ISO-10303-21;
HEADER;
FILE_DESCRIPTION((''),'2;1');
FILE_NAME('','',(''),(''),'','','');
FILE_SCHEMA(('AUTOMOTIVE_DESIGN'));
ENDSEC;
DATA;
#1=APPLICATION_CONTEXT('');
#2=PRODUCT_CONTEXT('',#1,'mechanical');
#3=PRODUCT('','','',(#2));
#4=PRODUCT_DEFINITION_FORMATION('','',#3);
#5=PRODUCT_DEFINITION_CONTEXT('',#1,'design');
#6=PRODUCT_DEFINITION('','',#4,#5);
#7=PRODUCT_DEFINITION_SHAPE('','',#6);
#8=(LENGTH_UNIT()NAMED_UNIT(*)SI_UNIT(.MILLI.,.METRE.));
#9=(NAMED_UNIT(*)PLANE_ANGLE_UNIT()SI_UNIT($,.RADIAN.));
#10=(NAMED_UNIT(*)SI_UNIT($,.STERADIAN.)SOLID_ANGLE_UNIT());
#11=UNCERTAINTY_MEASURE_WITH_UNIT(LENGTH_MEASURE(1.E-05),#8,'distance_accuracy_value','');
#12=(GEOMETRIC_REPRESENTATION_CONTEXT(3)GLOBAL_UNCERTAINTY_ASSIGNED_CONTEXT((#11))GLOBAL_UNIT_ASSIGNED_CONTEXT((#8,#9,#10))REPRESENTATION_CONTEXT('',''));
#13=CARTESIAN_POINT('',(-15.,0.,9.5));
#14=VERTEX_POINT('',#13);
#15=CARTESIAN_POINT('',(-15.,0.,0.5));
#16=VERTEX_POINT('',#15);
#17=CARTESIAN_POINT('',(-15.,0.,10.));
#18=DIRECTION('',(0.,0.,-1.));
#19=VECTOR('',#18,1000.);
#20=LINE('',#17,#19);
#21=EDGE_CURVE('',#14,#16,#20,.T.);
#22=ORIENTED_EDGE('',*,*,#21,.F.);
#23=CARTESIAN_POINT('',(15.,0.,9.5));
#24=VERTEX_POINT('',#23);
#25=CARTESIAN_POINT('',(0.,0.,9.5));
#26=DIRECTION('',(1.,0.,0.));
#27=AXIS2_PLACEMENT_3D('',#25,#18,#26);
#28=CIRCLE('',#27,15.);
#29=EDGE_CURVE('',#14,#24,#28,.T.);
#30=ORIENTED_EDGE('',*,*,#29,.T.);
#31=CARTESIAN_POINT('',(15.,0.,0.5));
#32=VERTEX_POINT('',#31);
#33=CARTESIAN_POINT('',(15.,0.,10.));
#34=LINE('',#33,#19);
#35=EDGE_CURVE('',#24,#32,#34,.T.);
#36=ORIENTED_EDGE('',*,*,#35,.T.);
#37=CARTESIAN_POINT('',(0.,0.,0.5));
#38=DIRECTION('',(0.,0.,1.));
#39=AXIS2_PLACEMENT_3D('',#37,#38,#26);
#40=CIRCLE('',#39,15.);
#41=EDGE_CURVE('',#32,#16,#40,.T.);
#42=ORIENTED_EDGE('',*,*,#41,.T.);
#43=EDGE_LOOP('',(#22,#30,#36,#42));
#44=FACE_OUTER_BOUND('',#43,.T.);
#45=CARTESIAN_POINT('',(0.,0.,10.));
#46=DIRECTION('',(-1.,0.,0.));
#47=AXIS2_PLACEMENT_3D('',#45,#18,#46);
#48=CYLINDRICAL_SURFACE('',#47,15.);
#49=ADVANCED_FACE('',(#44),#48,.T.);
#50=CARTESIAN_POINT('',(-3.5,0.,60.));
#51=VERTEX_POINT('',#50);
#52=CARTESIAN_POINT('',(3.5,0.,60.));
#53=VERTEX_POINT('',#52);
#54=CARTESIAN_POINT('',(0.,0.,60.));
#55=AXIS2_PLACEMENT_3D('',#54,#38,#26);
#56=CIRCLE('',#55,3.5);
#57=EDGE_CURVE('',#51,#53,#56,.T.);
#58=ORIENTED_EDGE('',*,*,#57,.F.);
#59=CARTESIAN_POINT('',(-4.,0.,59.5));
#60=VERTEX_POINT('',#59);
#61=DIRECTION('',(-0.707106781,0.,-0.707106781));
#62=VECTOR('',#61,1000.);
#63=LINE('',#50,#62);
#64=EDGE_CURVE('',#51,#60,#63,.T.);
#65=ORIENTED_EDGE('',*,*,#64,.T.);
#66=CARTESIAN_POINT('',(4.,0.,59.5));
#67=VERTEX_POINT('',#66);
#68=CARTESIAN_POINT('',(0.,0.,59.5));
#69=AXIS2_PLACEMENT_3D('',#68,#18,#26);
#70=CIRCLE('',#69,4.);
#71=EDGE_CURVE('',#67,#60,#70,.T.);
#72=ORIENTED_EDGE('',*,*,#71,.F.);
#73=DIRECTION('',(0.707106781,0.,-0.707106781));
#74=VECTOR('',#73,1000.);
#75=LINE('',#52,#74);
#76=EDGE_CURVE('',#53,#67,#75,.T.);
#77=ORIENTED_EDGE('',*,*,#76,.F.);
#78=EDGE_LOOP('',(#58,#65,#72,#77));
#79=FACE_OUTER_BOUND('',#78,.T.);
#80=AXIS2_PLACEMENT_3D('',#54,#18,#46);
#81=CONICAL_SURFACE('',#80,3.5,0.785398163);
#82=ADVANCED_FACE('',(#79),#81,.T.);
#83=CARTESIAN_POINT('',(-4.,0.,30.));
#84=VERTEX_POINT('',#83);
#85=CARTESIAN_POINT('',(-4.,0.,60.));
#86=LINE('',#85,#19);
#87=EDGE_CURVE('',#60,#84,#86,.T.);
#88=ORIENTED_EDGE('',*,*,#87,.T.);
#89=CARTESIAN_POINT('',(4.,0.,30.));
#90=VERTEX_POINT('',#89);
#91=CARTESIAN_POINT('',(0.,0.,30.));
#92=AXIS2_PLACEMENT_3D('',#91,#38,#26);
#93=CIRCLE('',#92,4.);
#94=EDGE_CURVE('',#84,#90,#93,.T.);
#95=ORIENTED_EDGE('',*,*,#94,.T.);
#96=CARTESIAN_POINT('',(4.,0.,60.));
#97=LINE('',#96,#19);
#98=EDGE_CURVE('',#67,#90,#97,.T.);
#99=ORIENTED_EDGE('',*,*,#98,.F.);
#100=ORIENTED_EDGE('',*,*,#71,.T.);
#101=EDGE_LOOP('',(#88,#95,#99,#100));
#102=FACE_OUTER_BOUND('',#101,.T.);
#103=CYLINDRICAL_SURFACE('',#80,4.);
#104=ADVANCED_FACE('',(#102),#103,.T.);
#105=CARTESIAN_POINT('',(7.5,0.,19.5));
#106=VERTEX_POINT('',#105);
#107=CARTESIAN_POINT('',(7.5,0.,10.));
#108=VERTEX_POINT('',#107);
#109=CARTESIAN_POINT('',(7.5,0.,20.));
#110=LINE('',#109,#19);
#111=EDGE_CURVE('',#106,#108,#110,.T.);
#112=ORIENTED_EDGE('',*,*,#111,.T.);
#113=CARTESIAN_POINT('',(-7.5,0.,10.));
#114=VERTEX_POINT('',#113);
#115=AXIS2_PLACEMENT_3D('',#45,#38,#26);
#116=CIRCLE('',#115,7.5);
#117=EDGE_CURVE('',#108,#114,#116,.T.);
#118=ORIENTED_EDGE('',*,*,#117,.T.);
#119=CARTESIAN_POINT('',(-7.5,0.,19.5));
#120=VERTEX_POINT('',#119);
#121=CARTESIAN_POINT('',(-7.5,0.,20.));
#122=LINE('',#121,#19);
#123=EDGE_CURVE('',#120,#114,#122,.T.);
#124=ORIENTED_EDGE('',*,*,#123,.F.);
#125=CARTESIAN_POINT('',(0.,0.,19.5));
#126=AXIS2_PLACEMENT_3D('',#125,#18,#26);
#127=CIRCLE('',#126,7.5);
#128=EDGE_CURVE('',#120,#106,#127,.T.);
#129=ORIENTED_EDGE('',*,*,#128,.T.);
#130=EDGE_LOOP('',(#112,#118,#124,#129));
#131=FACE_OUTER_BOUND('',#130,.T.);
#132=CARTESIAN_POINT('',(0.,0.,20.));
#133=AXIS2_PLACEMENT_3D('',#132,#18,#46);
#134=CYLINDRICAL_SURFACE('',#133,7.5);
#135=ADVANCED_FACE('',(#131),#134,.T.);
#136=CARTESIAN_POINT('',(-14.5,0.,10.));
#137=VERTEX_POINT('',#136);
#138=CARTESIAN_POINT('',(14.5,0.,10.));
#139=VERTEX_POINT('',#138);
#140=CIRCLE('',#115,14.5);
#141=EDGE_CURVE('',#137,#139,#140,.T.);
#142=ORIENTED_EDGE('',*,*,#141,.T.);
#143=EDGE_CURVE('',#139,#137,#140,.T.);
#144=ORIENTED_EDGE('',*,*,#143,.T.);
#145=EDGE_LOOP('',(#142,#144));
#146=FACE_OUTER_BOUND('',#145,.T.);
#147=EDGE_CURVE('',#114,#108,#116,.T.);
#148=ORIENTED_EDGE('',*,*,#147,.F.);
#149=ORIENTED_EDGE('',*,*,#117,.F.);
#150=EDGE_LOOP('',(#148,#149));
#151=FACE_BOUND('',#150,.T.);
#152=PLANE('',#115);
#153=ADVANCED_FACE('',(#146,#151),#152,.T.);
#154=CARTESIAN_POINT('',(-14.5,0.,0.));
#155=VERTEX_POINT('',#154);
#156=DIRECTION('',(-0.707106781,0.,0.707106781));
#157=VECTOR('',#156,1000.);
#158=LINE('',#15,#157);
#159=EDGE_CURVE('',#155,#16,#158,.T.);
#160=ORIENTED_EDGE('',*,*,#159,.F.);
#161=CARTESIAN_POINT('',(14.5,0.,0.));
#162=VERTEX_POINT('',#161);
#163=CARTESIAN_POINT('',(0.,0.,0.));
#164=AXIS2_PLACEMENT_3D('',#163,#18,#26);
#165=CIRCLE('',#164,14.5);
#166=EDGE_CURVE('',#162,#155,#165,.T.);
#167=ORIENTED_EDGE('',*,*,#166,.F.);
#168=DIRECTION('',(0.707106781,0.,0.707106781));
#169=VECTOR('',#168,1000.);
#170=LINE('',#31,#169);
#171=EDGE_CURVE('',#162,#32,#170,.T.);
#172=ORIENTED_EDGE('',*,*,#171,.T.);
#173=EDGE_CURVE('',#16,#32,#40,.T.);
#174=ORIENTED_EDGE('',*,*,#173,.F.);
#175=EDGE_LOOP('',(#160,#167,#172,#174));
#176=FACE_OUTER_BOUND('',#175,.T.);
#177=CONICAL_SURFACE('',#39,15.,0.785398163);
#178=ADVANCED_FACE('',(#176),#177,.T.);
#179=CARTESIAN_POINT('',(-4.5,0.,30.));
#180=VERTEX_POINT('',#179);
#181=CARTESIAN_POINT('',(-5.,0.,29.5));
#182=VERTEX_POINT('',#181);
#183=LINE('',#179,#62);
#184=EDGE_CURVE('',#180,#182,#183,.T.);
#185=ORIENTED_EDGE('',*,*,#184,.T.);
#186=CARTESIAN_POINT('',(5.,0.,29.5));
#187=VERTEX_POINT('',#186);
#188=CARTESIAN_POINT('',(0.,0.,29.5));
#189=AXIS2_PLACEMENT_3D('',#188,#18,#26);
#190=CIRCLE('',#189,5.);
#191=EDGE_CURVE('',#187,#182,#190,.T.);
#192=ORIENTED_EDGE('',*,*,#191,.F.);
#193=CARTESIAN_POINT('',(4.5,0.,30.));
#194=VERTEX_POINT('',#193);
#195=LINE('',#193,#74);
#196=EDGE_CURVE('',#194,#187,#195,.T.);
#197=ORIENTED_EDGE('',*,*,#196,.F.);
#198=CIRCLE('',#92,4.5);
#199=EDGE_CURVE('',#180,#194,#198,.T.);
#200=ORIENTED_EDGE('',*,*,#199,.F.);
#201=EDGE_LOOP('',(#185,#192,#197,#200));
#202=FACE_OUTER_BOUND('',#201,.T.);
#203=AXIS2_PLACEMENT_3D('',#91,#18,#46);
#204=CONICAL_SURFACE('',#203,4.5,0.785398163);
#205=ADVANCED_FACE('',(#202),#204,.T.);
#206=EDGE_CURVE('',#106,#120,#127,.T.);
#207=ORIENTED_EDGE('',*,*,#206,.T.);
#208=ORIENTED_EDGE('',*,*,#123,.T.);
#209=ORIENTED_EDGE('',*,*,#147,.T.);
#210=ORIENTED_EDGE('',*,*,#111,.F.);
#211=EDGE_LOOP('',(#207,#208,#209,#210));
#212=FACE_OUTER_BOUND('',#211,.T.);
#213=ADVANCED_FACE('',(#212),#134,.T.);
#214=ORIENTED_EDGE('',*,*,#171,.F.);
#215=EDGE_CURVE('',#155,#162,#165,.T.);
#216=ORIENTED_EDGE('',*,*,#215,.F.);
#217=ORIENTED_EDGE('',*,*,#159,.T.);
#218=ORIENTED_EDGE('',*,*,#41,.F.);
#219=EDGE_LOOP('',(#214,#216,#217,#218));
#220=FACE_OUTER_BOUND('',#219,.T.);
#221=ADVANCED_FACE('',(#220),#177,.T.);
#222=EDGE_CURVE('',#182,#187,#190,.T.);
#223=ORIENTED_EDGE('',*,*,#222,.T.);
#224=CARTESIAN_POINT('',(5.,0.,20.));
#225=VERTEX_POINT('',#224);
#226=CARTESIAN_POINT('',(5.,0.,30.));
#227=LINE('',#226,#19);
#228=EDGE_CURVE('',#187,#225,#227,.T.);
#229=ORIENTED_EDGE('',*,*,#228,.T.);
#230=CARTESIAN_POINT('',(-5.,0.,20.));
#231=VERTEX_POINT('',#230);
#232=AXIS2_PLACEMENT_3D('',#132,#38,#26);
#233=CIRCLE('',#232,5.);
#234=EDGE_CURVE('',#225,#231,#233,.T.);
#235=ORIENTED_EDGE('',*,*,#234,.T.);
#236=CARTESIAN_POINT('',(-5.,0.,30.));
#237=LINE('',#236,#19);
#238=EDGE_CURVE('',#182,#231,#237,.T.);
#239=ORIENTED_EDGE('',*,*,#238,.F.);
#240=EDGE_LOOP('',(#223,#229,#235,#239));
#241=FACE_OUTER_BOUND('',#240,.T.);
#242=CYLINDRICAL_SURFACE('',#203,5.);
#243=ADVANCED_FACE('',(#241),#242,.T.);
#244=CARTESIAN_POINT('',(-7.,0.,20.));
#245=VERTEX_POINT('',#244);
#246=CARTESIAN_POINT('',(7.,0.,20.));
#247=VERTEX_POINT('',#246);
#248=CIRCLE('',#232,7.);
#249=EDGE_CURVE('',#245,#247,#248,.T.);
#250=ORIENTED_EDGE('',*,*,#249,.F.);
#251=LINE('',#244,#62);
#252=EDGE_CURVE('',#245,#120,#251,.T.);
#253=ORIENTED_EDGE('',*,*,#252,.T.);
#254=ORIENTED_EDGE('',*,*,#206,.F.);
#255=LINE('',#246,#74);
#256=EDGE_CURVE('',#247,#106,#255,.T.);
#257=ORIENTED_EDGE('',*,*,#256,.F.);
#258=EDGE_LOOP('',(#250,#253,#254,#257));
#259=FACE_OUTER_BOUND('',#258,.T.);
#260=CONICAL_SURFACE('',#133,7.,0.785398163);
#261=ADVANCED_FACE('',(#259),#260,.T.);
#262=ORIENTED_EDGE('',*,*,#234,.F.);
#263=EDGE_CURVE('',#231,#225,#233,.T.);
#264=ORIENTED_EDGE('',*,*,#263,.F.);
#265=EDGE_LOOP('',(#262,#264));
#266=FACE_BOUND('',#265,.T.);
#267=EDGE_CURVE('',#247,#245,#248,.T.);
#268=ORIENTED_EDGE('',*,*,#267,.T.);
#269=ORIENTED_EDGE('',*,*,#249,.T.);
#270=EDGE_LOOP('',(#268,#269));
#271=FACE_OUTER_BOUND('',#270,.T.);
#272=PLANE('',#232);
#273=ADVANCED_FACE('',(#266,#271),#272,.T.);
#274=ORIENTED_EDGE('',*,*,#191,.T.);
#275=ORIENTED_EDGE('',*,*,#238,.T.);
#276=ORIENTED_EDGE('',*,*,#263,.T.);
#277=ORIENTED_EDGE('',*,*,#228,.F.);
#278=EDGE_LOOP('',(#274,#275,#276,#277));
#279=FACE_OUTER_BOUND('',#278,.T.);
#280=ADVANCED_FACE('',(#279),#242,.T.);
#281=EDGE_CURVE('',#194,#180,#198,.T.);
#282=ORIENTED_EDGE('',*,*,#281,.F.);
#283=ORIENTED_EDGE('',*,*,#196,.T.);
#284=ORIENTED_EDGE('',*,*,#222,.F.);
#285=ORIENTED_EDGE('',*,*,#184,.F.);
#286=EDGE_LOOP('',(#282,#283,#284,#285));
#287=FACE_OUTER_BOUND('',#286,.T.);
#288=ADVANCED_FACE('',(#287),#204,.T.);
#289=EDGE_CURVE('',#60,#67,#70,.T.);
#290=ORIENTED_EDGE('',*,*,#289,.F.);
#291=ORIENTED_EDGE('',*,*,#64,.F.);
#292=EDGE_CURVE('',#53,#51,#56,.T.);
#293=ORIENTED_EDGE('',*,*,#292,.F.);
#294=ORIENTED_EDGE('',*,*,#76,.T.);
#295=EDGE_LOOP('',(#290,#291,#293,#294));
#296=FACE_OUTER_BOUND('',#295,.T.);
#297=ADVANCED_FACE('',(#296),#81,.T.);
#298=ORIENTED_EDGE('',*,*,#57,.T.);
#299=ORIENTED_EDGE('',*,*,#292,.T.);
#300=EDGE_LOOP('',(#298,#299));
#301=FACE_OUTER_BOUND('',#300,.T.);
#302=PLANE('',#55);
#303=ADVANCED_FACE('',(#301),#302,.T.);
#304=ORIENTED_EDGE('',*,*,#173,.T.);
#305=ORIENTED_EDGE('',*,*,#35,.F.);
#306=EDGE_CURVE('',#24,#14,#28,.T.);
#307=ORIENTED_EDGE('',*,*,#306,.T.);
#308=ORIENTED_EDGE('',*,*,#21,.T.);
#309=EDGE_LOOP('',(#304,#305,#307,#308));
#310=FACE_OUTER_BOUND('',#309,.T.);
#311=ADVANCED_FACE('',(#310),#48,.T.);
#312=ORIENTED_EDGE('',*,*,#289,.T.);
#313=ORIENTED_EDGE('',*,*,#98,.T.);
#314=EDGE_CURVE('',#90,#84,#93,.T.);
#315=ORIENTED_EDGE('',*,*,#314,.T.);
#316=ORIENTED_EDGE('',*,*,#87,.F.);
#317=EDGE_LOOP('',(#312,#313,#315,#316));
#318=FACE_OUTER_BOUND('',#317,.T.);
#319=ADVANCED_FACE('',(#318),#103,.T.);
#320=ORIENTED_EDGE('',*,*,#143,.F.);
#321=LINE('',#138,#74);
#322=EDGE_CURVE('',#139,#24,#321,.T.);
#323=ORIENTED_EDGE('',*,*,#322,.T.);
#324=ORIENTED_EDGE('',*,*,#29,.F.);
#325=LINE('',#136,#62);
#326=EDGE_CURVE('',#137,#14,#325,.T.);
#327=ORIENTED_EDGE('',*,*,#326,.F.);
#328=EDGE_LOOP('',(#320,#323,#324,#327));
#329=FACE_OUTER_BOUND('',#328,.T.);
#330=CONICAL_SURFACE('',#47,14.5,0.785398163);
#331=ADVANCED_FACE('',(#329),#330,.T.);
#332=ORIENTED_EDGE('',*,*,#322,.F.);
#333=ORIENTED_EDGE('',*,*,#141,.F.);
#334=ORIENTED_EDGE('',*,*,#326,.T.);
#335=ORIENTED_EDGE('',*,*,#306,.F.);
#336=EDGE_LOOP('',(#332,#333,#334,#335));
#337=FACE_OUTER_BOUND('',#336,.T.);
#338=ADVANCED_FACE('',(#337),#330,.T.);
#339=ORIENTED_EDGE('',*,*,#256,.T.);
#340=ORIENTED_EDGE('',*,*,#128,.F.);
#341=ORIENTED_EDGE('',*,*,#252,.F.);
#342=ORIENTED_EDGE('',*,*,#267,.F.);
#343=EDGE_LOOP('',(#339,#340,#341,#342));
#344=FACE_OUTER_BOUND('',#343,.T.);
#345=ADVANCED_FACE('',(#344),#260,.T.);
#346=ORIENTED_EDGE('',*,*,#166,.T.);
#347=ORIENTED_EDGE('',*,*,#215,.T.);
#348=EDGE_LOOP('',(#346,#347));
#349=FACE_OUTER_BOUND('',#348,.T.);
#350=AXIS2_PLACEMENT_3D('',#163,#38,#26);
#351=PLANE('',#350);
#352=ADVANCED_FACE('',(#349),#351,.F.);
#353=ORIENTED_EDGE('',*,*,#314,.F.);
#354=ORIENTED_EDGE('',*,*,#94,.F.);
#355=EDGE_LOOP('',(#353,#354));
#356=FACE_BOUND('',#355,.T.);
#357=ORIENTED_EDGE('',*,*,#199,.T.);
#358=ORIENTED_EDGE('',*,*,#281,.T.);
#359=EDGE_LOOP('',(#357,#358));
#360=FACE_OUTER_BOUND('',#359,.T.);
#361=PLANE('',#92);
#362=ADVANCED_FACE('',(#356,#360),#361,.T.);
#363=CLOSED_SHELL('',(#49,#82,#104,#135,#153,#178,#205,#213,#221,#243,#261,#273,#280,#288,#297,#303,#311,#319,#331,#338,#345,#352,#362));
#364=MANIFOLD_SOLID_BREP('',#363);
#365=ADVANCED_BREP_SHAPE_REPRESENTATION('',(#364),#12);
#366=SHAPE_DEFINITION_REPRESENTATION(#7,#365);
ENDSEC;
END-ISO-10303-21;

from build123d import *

# Parameters (mm, degrees)
SKETCH1_R           = 15
BOSS_EXTRUDE1_DEPTH = 10
SKETCH2_R           = 7.5
BOSS_EXTRUDE2_DEPTH = 10
SKETCH3_R           = 4
BOSS_EXTRUDE3_DEPTH = 40
SKETCH4_R           = 5
BOSS_EXTRUDE4_DEPTH = 10
CHAMFER1_SIZE       = 0.5


with BuildPart() as part:
    # Sketch1 → Boss-Extrude1 (new body)
    with BuildSketch(Plane.XY):
        Circle(SKETCH1_R)
    extrude(amount=BOSS_EXTRUDE1_DEPTH)

    # Sketch2 → Boss-Extrude2 (add)
    with BuildSketch(Plane.XY.offset(10)):
        Circle(SKETCH2_R)
    extrude(amount=BOSS_EXTRUDE2_DEPTH)

    # Sketch3 → Boss-Extrude3 (add)
    with BuildSketch(Plane.XY.offset(20)):
        Circle(SKETCH3_R)
    extrude(amount=BOSS_EXTRUDE3_DEPTH)

    # Sketch4 → Boss-Extrude4 (add)
    with BuildSketch(Plane.XY.offset(20)):
        Circle(SKETCH4_R)
    extrude(amount=BOSS_EXTRUDE4_DEPTH)

    # Chamfer1
    chamfer1_edges = [part.edges().sort_by_distance(p)[0] for p in [
        (-4, 0, 60),
        (-5, 0, 30),
        (-15, 0, 0),
        (-15, 0, 10),
        (-7.5, 0, 20),
    ]]
    chamfer(chamfer1_edges, length=CHAMFER1_SIZE)


solid = part.part
